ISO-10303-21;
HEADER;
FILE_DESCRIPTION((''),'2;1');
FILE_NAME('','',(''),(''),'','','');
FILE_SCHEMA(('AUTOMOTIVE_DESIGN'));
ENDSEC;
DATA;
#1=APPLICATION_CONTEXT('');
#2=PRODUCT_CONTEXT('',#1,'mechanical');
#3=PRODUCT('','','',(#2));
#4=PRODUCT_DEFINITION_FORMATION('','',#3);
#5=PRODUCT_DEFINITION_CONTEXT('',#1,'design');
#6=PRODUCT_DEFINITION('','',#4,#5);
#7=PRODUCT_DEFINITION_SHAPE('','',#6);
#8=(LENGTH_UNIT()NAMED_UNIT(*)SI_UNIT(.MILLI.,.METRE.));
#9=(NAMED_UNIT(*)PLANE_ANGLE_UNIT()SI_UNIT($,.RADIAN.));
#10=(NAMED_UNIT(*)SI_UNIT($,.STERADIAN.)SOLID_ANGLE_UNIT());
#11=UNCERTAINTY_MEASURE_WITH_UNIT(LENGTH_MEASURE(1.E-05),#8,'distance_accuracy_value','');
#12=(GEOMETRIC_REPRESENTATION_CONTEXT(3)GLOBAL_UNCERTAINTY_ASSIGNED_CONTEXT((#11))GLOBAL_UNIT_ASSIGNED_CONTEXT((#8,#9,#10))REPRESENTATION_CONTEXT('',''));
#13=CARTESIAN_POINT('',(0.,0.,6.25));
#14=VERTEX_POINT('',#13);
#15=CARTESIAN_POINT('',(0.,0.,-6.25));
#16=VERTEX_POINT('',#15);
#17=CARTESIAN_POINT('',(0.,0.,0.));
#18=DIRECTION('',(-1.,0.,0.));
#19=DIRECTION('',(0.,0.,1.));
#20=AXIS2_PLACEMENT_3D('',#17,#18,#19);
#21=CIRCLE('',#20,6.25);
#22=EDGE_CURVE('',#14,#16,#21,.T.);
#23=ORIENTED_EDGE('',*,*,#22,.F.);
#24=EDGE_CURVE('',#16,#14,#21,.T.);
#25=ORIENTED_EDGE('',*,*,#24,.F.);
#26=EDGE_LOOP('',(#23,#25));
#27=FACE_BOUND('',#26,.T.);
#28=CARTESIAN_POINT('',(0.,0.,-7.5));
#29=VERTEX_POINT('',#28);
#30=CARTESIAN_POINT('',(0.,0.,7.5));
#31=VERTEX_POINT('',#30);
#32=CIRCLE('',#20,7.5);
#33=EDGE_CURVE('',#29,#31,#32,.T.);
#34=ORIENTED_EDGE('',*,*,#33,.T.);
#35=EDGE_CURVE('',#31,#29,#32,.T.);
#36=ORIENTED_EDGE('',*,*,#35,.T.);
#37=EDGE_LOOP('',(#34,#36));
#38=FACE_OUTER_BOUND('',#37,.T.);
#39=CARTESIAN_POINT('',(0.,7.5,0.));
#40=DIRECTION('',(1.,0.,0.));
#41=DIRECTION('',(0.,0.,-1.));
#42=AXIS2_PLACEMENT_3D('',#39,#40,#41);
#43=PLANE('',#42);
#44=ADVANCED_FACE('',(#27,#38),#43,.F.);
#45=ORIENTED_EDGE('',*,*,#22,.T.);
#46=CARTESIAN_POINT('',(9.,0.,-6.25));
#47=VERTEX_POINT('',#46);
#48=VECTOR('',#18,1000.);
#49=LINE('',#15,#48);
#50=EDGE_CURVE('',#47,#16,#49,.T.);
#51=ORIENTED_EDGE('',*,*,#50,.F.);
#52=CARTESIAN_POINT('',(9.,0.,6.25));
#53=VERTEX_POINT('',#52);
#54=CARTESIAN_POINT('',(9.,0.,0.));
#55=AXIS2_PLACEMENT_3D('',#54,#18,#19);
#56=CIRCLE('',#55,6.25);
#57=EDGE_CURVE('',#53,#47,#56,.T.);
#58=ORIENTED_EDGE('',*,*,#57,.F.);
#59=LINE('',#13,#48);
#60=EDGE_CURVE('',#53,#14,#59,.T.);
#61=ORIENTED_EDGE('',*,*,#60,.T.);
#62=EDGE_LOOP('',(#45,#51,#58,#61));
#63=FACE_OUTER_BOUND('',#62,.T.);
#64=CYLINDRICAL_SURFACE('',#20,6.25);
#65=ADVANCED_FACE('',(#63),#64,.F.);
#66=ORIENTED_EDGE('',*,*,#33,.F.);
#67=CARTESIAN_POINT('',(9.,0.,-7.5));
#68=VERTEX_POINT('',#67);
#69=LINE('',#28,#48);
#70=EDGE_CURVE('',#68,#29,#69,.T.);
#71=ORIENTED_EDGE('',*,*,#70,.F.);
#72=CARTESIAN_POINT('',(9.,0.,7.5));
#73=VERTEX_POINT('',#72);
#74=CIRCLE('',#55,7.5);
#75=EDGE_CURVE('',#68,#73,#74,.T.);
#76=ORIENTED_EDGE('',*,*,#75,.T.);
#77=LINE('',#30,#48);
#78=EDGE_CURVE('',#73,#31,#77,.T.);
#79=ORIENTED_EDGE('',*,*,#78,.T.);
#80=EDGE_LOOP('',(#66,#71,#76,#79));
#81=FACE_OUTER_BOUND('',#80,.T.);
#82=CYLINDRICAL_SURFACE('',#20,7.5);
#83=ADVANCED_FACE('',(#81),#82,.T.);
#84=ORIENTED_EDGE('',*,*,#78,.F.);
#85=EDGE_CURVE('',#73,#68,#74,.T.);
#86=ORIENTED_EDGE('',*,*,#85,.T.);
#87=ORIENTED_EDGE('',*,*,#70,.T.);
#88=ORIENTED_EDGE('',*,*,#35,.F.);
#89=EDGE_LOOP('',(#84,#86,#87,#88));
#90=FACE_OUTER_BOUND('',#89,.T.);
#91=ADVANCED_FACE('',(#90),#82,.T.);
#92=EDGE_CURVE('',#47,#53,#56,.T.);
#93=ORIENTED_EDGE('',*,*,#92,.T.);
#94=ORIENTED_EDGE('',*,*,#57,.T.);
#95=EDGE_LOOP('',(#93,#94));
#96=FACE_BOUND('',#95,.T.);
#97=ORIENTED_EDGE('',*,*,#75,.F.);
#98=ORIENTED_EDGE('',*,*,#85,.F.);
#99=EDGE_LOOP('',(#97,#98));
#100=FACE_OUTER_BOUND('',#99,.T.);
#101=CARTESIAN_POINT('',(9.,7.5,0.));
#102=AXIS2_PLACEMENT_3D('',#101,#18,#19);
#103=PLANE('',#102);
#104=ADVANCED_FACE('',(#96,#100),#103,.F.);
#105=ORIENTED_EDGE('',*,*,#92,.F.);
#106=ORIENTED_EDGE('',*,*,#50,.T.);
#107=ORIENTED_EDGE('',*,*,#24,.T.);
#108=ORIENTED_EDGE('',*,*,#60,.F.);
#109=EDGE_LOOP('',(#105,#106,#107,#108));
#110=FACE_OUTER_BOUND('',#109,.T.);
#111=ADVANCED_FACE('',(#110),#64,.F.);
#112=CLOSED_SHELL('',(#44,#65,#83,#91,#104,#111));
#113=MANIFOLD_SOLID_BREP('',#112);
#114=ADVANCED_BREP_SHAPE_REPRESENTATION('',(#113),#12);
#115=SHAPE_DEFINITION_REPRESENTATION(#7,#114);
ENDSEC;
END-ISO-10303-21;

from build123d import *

# Parameters (mm, degrees)
SKETCH1_W = 9
SKETCH1_H = 1.25


with BuildPart() as part:
    # Sketch1 → Revolve1 (revolve)
    with BuildSketch(Plane.XY, mode=Mode.PRIVATE) as revolve1_sk:
        with Locations((4.5, 6.875)):
            Rectangle(SKETCH1_W, SKETCH1_H)
    revolve(revolve1_sk.sketch.rotate(Axis((0, 0, 0), (1, 0, 0)), 90), axis=Axis((0, 0, 0), (1, 0, 0)))


solid = part.part
